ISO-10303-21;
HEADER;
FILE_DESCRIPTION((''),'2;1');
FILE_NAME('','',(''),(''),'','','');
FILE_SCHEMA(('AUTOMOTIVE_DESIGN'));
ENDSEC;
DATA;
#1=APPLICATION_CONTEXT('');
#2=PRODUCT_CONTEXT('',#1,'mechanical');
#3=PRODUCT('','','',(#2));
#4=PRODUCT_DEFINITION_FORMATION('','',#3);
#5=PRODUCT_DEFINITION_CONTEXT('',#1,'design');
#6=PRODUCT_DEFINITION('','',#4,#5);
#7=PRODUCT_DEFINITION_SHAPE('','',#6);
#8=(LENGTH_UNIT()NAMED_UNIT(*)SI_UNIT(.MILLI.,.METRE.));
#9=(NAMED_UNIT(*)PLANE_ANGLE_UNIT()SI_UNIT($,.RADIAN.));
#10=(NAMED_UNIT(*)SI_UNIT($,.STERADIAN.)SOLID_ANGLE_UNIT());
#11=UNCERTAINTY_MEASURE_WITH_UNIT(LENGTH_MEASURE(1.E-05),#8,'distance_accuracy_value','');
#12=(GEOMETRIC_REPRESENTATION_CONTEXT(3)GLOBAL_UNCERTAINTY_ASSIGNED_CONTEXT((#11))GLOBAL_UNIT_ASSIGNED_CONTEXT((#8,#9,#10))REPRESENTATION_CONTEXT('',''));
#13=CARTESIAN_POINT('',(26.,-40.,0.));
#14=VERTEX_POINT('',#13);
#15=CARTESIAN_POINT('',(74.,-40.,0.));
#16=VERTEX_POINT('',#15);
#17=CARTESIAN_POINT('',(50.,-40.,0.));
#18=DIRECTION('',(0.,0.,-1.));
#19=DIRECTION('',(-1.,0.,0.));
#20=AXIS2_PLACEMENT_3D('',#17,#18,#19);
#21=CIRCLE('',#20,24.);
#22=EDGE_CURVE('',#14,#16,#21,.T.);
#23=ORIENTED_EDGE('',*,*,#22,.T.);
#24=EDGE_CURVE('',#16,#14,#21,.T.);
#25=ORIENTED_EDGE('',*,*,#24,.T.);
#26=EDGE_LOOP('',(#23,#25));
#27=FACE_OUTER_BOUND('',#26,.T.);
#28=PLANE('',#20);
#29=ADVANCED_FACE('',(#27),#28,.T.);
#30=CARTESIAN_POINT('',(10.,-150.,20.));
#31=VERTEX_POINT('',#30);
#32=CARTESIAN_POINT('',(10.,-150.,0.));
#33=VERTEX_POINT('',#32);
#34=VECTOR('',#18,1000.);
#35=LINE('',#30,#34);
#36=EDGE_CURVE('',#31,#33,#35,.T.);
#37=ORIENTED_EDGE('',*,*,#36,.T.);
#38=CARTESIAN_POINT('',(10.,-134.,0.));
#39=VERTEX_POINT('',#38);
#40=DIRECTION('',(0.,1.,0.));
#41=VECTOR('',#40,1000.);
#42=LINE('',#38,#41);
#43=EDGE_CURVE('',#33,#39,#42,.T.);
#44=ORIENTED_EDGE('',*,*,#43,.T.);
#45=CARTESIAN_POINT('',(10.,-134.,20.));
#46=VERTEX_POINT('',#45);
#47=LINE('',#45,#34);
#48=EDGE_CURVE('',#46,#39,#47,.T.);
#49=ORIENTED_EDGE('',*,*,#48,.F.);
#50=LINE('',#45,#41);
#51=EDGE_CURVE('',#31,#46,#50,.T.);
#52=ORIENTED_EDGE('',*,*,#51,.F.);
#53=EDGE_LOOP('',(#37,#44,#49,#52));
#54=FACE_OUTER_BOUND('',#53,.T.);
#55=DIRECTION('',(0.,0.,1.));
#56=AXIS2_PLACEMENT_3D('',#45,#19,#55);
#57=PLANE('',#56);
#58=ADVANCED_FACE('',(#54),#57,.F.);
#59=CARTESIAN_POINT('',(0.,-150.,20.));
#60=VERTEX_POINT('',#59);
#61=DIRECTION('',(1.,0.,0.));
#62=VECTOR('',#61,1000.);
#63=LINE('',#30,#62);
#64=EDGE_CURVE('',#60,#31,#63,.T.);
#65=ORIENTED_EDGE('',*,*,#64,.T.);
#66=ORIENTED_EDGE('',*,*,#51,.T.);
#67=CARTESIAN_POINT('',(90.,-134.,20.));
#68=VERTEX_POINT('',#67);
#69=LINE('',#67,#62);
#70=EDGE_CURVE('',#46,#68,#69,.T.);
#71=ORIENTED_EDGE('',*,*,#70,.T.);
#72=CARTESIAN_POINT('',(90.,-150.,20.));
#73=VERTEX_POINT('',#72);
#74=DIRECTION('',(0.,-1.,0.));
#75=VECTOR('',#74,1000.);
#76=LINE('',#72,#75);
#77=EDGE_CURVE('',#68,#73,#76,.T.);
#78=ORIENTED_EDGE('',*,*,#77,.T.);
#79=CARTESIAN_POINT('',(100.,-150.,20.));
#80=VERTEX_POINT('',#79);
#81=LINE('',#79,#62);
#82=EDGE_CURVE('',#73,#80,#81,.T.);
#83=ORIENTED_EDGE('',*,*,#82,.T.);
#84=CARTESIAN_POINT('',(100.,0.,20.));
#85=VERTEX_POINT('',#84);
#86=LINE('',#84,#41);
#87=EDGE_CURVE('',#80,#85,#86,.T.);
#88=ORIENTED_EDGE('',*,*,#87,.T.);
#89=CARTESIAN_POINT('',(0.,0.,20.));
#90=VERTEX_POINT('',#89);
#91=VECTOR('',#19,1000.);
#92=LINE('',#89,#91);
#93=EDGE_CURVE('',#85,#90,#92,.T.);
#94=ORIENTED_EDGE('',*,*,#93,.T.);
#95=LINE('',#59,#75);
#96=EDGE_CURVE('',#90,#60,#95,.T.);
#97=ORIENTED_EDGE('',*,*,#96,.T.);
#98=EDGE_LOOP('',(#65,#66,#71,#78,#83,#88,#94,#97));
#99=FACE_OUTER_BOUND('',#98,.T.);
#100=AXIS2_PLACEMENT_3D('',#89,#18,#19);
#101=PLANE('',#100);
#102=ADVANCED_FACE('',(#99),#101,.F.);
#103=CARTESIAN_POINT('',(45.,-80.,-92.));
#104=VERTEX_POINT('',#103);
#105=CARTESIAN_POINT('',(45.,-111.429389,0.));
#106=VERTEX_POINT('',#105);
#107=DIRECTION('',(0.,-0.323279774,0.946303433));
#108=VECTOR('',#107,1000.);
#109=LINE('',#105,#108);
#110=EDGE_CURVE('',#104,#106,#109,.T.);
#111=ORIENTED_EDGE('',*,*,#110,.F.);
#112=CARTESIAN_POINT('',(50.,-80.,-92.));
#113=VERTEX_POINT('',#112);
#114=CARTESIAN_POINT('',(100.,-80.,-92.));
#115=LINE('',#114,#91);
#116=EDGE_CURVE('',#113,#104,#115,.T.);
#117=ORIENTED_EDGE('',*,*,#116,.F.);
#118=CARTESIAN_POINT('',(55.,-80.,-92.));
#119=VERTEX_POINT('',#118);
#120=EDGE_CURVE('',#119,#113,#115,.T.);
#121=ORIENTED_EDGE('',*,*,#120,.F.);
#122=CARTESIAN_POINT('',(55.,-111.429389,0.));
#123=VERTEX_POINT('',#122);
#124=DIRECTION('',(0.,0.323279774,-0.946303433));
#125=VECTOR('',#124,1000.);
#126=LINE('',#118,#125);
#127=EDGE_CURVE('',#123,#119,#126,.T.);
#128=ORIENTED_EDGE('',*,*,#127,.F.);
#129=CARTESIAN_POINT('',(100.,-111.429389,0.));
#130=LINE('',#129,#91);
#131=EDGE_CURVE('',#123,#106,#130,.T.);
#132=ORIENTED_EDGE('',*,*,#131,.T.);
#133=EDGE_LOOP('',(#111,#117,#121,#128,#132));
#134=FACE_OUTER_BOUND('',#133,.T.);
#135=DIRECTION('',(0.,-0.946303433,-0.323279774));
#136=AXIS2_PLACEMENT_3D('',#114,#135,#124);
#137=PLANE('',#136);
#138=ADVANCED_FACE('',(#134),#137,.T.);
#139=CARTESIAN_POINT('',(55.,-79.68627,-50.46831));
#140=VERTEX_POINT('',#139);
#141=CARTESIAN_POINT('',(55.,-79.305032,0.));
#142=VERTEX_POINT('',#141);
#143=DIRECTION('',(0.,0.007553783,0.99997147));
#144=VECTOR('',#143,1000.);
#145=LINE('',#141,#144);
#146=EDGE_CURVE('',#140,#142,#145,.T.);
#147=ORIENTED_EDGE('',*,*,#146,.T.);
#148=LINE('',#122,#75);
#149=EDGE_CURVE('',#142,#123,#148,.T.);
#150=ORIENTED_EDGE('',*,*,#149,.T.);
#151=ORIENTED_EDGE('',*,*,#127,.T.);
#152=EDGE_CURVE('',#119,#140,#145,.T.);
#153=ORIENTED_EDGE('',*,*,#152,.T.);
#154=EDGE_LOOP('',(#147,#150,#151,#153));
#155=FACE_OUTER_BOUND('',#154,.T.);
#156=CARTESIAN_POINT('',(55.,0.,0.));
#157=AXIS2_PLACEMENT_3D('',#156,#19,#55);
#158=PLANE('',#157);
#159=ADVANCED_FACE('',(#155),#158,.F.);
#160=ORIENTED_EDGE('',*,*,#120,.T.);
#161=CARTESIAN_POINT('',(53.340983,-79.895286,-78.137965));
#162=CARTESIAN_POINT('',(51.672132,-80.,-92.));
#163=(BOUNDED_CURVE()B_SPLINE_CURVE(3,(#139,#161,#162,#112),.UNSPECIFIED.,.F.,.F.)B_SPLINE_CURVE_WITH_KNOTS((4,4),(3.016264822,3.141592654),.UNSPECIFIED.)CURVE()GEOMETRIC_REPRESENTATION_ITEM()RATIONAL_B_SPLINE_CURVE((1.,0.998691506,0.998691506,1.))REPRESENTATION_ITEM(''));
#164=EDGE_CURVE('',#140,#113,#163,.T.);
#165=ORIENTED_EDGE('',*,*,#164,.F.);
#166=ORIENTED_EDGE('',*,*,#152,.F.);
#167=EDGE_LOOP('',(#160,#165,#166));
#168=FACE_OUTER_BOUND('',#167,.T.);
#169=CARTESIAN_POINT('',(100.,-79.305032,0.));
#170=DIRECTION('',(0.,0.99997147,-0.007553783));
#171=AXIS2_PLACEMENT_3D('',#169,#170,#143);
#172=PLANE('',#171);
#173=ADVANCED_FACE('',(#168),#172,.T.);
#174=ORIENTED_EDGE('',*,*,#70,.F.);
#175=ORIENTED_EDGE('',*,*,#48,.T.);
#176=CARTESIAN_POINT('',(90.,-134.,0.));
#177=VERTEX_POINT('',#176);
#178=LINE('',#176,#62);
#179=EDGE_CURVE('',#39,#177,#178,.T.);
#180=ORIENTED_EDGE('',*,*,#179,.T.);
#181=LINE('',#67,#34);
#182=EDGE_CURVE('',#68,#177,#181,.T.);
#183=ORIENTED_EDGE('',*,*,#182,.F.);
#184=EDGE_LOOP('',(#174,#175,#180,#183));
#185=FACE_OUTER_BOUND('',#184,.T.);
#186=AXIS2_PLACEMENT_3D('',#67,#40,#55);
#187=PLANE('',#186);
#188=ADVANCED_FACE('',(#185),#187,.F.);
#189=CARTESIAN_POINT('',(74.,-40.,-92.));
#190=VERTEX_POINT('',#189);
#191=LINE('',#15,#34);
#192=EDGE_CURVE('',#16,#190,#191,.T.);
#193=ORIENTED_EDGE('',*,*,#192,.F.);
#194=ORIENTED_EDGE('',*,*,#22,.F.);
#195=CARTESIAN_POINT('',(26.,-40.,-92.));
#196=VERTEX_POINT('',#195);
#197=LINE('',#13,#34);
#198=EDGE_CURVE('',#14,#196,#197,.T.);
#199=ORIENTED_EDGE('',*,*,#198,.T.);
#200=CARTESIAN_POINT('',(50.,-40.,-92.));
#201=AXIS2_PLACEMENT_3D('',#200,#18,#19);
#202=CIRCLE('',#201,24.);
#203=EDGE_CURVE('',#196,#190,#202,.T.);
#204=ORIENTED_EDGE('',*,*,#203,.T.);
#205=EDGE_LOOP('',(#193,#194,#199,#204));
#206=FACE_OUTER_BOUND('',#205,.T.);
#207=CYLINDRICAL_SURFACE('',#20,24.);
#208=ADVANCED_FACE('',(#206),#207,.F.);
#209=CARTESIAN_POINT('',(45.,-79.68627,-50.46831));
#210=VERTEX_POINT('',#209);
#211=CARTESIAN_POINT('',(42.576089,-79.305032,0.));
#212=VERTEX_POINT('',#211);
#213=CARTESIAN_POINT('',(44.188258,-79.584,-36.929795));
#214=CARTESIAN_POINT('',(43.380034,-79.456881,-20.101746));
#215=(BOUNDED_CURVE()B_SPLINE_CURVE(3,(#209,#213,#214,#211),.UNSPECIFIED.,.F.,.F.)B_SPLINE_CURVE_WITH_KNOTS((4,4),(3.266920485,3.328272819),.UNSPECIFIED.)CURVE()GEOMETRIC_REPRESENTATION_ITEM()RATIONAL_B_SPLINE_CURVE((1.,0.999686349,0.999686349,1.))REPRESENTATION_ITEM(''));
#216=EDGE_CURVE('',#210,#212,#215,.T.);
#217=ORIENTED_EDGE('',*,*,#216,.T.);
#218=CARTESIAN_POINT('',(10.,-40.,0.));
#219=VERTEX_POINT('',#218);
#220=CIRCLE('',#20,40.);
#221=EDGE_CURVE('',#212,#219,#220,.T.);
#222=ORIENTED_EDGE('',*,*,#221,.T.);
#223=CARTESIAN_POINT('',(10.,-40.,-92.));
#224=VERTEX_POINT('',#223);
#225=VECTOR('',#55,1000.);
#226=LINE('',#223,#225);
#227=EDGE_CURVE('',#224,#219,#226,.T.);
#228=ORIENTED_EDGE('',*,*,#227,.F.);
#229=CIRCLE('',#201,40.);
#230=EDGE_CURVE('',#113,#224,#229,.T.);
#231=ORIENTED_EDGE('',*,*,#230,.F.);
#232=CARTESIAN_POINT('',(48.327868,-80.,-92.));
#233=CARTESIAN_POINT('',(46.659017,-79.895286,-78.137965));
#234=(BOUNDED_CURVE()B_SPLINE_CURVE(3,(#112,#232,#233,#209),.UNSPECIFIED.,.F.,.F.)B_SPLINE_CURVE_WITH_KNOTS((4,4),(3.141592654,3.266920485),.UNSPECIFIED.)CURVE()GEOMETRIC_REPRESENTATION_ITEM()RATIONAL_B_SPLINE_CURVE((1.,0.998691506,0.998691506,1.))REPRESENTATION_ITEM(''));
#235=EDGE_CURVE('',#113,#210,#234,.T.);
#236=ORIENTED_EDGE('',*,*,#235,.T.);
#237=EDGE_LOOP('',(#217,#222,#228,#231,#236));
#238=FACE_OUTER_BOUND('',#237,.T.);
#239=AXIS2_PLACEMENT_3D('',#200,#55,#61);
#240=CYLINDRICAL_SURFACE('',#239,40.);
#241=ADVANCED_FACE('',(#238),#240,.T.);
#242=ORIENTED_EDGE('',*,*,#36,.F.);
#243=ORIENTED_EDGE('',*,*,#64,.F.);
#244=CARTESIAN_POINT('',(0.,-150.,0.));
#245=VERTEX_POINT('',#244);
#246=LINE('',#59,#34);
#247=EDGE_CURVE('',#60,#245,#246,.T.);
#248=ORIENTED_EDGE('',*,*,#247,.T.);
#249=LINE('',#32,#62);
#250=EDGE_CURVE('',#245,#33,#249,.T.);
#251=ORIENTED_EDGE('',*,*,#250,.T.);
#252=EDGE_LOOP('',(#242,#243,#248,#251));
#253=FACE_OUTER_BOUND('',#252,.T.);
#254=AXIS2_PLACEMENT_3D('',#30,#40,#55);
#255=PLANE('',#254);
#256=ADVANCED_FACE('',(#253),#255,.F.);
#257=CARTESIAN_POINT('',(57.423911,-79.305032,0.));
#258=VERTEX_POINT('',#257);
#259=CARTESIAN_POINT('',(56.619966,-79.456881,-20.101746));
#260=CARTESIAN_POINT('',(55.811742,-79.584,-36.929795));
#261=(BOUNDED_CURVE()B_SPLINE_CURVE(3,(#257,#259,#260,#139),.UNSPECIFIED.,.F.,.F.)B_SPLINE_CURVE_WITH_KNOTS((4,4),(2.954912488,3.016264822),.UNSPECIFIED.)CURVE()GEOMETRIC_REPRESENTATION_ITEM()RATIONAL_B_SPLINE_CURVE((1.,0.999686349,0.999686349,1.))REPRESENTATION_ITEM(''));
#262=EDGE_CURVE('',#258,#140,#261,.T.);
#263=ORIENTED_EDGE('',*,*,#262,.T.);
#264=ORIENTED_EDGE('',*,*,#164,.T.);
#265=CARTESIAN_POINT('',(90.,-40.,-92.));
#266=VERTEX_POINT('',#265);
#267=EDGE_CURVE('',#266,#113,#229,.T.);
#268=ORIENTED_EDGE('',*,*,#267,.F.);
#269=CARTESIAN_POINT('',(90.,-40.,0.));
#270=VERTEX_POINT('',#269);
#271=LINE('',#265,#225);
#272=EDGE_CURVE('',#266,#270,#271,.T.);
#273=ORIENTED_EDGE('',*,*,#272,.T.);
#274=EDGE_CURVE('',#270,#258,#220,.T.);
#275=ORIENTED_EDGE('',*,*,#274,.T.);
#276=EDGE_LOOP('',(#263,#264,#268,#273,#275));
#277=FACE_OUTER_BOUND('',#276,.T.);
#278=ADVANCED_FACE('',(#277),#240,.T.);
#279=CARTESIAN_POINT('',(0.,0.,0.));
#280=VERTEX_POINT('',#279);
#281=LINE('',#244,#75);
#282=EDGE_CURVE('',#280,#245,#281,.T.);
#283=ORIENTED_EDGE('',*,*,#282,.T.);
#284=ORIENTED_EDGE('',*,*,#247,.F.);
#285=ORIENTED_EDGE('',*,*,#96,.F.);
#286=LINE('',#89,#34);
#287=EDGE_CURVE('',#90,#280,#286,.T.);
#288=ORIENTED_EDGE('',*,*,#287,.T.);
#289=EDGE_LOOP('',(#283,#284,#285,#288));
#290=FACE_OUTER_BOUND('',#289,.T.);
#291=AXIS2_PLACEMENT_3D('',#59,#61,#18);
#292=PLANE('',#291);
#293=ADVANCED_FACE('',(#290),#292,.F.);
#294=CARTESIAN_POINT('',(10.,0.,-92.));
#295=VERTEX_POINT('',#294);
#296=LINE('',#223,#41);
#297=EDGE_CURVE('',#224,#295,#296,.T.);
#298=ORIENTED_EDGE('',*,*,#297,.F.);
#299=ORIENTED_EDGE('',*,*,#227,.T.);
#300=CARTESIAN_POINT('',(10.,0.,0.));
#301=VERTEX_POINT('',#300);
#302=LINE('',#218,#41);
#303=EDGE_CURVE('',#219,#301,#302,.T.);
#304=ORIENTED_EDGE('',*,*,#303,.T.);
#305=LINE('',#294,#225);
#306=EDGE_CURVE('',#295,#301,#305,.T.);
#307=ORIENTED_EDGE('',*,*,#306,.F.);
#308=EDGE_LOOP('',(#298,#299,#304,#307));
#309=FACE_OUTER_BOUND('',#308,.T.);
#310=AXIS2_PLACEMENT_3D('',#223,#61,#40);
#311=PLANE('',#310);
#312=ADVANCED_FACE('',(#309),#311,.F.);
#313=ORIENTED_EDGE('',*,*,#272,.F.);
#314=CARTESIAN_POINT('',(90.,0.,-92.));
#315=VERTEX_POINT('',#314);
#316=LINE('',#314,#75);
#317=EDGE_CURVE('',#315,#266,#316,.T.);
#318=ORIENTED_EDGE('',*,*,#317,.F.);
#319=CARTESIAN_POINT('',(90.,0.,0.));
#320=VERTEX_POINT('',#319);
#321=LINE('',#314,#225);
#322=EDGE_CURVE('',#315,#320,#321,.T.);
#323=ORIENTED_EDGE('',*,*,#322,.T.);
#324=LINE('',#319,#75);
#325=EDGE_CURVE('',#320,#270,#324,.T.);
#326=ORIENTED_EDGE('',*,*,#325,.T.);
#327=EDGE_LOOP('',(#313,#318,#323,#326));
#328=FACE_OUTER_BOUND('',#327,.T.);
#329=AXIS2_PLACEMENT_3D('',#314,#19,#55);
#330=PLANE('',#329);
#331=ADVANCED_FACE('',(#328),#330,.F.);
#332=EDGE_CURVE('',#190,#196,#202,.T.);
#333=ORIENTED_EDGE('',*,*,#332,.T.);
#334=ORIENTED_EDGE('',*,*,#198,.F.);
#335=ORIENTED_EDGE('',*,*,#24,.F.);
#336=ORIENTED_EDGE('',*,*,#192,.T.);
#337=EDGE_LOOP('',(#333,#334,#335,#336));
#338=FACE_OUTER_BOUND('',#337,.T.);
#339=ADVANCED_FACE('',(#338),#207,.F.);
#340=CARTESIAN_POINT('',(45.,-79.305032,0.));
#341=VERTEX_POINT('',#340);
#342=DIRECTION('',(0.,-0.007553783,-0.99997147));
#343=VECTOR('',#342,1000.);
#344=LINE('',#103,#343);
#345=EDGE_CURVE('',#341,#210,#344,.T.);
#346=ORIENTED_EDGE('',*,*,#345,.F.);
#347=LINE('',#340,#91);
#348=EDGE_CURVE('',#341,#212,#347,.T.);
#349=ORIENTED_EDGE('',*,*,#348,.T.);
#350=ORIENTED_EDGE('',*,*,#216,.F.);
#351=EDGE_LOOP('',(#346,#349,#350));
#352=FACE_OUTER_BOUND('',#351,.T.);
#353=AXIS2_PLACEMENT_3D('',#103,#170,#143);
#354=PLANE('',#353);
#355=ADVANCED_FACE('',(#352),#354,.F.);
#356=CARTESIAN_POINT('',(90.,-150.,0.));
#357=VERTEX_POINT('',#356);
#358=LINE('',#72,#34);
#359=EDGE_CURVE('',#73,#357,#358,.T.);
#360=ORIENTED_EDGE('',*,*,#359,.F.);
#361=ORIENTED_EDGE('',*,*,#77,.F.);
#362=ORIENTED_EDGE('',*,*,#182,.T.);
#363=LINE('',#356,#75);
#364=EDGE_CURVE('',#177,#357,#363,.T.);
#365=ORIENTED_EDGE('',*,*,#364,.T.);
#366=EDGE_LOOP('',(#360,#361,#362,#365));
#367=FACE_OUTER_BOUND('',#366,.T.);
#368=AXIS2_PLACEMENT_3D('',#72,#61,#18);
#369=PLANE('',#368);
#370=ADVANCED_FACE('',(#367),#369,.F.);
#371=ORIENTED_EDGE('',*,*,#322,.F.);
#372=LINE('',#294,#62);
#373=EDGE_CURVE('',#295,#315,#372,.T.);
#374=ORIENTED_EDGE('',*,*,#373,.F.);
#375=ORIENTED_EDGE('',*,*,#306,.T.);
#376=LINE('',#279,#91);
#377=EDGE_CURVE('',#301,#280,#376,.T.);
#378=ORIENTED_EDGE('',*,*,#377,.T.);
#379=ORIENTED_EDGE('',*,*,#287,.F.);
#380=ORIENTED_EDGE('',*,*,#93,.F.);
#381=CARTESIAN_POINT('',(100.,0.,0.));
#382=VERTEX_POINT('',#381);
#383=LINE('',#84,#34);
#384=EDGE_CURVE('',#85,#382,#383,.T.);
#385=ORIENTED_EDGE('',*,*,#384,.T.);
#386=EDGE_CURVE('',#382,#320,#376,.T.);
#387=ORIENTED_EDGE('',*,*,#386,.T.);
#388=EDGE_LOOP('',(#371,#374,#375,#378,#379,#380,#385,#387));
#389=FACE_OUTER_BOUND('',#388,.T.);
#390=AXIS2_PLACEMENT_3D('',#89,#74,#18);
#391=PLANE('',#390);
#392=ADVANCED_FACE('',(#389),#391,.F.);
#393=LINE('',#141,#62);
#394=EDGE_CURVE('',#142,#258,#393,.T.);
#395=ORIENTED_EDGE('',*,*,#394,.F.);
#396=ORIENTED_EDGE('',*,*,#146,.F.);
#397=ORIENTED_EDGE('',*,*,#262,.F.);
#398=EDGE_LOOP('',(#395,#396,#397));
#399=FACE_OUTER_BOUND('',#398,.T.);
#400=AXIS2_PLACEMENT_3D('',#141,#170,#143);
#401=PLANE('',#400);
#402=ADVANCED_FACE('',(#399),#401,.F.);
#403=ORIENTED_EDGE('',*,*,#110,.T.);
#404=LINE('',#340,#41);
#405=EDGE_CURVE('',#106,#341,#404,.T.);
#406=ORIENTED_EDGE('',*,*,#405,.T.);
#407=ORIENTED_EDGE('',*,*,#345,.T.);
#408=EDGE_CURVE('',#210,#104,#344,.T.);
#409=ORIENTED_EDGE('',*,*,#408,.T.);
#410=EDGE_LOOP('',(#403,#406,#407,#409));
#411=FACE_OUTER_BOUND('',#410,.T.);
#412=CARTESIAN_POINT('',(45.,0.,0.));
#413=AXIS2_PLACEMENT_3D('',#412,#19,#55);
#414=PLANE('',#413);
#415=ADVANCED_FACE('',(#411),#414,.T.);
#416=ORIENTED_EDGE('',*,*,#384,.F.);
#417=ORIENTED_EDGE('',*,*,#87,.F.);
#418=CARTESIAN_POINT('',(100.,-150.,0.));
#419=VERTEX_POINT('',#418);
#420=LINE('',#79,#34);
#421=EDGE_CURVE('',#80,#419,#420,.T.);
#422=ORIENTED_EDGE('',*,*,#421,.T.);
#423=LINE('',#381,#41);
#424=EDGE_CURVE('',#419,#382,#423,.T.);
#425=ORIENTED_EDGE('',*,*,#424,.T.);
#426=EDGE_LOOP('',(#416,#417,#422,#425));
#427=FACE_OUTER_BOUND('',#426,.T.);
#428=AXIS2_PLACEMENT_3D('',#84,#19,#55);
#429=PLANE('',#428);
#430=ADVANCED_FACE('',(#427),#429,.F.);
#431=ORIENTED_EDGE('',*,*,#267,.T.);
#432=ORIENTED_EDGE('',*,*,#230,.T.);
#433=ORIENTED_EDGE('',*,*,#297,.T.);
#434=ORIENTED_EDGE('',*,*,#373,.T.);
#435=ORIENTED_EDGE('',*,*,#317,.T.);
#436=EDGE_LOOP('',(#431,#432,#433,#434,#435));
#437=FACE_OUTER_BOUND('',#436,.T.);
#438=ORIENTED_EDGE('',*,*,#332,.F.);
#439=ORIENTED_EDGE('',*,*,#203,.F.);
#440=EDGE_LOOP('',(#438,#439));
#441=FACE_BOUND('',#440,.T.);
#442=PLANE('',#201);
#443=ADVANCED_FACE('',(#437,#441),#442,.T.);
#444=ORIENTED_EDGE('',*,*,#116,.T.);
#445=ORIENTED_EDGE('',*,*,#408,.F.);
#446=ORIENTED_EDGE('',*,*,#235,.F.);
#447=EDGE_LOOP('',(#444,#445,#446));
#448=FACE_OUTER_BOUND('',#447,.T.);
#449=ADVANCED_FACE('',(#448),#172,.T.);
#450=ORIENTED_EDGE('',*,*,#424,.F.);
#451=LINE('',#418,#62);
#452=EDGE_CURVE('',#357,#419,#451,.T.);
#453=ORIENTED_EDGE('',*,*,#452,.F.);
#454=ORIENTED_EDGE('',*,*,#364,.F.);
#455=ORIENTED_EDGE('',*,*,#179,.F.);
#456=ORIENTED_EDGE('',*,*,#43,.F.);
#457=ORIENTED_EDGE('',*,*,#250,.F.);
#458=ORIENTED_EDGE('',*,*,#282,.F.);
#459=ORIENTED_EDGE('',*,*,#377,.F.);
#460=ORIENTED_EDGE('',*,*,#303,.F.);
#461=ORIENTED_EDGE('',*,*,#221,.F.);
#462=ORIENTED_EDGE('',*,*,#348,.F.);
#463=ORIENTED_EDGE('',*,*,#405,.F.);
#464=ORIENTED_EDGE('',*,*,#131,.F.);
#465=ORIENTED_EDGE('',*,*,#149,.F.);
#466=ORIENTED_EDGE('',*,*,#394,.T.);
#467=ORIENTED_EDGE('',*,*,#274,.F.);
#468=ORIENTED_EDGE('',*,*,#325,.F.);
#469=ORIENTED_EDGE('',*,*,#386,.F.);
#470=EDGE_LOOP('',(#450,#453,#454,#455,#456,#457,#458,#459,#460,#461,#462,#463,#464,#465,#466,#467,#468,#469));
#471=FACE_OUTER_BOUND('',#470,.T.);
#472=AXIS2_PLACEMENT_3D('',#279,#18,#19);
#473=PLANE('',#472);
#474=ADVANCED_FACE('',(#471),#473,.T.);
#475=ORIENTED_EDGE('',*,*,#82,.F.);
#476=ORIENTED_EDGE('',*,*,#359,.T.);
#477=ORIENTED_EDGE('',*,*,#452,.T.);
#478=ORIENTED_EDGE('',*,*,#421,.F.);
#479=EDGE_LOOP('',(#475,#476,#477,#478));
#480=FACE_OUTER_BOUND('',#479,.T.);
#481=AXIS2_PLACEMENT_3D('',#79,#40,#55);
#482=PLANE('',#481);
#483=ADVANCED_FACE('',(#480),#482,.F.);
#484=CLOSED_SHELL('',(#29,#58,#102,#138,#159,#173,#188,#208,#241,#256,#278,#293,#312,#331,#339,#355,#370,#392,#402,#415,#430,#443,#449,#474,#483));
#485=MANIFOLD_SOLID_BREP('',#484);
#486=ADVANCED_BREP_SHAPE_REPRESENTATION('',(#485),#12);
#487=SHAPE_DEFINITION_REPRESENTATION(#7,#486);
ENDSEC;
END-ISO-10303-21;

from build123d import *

# Parameters (mm, degrees)
BASE_PLATE_20MM_DEPTH   = 20
BLOCK_92MM_DEPTH        = 92
RELIEF_CUT_SKETCH_R     = 24
RELIEF_CUT_DEPTH        = 92
GUSSET_100MM_DEPTH      = 100
GUSSET_TRIM_CUT_1_DEPTH = 45
GUSSET_TRIM_CUT_2_DEPTH = 45


with BuildPart() as part:
    # Base Plate Sketch → Base Plate 20mm (new body)
    with BuildSketch(Plane.XY):
        Polygon((0, 0), (100, 0), (100, -150), (90, -150), (90, -134), (10, -134), (10, -150), (0, -150), align=None)
    extrude(amount=BASE_PLATE_20MM_DEPTH)

    # Block Sketch → Block 92mm (add)
    with BuildSketch(Plane(origin=(0, 0, 0), x_dir=(-1, 0, 0), z_dir=(0, 0, -1))):
        with BuildLine():
            Line((-10, -40), (-10, 0))
            Line((-10, 0), (-90, 0))
            Line((-90, 0), (-90, -40))
            ThreePointArc((-90, -40), (-50, -80), (-10, -40))
        make_face()
    extrude(amount=BLOCK_92MM_DEPTH)

    # Relief Cut Sketch → Relief Cut (cut)
    with BuildSketch(Plane(origin=(0, 0, -92), x_dir=(-1, 0, 0), z_dir=(0, 0, -1))):
        with Locations((-50, -40)):
            Circle(RELIEF_CUT_SKETCH_R)
    extrude(amount=-RELIEF_CUT_DEPTH, mode=Mode.SUBTRACT)

    # Gusset Sketch → Gusset 100mm (add)
    with BuildSketch(Plane.ZY):
        Polygon((-92, -80), (0, -111.42938948), (0, -79.30503211), align=None)
    extrude(amount=-GUSSET_100MM_DEPTH)

    # Gusset Trim Sketch 1 → Gusset Trim Cut 1 (cut)
    with BuildSketch(Plane.ZY):
        Polygon((-92, -80), (0, -79.30503211), (0, -111.42938948), align=None)
    extrude(amount=-GUSSET_TRIM_CUT_1_DEPTH, mode=Mode.SUBTRACT)

    # Gusset Trim Sketch 2 → Gusset Trim Cut 2 (cut)
    with BuildSketch(Plane(origin=(100, 0, 0), x_dir=(0, 0, -1), z_dir=(1, 0, 0))):
        Polygon((0, -79.30503211), (92, -80), (0, -111.42938948), align=None)
    extrude(amount=-GUSSET_TRIM_CUT_2_DEPTH, mode=Mode.SUBTRACT)


solid = part.part
